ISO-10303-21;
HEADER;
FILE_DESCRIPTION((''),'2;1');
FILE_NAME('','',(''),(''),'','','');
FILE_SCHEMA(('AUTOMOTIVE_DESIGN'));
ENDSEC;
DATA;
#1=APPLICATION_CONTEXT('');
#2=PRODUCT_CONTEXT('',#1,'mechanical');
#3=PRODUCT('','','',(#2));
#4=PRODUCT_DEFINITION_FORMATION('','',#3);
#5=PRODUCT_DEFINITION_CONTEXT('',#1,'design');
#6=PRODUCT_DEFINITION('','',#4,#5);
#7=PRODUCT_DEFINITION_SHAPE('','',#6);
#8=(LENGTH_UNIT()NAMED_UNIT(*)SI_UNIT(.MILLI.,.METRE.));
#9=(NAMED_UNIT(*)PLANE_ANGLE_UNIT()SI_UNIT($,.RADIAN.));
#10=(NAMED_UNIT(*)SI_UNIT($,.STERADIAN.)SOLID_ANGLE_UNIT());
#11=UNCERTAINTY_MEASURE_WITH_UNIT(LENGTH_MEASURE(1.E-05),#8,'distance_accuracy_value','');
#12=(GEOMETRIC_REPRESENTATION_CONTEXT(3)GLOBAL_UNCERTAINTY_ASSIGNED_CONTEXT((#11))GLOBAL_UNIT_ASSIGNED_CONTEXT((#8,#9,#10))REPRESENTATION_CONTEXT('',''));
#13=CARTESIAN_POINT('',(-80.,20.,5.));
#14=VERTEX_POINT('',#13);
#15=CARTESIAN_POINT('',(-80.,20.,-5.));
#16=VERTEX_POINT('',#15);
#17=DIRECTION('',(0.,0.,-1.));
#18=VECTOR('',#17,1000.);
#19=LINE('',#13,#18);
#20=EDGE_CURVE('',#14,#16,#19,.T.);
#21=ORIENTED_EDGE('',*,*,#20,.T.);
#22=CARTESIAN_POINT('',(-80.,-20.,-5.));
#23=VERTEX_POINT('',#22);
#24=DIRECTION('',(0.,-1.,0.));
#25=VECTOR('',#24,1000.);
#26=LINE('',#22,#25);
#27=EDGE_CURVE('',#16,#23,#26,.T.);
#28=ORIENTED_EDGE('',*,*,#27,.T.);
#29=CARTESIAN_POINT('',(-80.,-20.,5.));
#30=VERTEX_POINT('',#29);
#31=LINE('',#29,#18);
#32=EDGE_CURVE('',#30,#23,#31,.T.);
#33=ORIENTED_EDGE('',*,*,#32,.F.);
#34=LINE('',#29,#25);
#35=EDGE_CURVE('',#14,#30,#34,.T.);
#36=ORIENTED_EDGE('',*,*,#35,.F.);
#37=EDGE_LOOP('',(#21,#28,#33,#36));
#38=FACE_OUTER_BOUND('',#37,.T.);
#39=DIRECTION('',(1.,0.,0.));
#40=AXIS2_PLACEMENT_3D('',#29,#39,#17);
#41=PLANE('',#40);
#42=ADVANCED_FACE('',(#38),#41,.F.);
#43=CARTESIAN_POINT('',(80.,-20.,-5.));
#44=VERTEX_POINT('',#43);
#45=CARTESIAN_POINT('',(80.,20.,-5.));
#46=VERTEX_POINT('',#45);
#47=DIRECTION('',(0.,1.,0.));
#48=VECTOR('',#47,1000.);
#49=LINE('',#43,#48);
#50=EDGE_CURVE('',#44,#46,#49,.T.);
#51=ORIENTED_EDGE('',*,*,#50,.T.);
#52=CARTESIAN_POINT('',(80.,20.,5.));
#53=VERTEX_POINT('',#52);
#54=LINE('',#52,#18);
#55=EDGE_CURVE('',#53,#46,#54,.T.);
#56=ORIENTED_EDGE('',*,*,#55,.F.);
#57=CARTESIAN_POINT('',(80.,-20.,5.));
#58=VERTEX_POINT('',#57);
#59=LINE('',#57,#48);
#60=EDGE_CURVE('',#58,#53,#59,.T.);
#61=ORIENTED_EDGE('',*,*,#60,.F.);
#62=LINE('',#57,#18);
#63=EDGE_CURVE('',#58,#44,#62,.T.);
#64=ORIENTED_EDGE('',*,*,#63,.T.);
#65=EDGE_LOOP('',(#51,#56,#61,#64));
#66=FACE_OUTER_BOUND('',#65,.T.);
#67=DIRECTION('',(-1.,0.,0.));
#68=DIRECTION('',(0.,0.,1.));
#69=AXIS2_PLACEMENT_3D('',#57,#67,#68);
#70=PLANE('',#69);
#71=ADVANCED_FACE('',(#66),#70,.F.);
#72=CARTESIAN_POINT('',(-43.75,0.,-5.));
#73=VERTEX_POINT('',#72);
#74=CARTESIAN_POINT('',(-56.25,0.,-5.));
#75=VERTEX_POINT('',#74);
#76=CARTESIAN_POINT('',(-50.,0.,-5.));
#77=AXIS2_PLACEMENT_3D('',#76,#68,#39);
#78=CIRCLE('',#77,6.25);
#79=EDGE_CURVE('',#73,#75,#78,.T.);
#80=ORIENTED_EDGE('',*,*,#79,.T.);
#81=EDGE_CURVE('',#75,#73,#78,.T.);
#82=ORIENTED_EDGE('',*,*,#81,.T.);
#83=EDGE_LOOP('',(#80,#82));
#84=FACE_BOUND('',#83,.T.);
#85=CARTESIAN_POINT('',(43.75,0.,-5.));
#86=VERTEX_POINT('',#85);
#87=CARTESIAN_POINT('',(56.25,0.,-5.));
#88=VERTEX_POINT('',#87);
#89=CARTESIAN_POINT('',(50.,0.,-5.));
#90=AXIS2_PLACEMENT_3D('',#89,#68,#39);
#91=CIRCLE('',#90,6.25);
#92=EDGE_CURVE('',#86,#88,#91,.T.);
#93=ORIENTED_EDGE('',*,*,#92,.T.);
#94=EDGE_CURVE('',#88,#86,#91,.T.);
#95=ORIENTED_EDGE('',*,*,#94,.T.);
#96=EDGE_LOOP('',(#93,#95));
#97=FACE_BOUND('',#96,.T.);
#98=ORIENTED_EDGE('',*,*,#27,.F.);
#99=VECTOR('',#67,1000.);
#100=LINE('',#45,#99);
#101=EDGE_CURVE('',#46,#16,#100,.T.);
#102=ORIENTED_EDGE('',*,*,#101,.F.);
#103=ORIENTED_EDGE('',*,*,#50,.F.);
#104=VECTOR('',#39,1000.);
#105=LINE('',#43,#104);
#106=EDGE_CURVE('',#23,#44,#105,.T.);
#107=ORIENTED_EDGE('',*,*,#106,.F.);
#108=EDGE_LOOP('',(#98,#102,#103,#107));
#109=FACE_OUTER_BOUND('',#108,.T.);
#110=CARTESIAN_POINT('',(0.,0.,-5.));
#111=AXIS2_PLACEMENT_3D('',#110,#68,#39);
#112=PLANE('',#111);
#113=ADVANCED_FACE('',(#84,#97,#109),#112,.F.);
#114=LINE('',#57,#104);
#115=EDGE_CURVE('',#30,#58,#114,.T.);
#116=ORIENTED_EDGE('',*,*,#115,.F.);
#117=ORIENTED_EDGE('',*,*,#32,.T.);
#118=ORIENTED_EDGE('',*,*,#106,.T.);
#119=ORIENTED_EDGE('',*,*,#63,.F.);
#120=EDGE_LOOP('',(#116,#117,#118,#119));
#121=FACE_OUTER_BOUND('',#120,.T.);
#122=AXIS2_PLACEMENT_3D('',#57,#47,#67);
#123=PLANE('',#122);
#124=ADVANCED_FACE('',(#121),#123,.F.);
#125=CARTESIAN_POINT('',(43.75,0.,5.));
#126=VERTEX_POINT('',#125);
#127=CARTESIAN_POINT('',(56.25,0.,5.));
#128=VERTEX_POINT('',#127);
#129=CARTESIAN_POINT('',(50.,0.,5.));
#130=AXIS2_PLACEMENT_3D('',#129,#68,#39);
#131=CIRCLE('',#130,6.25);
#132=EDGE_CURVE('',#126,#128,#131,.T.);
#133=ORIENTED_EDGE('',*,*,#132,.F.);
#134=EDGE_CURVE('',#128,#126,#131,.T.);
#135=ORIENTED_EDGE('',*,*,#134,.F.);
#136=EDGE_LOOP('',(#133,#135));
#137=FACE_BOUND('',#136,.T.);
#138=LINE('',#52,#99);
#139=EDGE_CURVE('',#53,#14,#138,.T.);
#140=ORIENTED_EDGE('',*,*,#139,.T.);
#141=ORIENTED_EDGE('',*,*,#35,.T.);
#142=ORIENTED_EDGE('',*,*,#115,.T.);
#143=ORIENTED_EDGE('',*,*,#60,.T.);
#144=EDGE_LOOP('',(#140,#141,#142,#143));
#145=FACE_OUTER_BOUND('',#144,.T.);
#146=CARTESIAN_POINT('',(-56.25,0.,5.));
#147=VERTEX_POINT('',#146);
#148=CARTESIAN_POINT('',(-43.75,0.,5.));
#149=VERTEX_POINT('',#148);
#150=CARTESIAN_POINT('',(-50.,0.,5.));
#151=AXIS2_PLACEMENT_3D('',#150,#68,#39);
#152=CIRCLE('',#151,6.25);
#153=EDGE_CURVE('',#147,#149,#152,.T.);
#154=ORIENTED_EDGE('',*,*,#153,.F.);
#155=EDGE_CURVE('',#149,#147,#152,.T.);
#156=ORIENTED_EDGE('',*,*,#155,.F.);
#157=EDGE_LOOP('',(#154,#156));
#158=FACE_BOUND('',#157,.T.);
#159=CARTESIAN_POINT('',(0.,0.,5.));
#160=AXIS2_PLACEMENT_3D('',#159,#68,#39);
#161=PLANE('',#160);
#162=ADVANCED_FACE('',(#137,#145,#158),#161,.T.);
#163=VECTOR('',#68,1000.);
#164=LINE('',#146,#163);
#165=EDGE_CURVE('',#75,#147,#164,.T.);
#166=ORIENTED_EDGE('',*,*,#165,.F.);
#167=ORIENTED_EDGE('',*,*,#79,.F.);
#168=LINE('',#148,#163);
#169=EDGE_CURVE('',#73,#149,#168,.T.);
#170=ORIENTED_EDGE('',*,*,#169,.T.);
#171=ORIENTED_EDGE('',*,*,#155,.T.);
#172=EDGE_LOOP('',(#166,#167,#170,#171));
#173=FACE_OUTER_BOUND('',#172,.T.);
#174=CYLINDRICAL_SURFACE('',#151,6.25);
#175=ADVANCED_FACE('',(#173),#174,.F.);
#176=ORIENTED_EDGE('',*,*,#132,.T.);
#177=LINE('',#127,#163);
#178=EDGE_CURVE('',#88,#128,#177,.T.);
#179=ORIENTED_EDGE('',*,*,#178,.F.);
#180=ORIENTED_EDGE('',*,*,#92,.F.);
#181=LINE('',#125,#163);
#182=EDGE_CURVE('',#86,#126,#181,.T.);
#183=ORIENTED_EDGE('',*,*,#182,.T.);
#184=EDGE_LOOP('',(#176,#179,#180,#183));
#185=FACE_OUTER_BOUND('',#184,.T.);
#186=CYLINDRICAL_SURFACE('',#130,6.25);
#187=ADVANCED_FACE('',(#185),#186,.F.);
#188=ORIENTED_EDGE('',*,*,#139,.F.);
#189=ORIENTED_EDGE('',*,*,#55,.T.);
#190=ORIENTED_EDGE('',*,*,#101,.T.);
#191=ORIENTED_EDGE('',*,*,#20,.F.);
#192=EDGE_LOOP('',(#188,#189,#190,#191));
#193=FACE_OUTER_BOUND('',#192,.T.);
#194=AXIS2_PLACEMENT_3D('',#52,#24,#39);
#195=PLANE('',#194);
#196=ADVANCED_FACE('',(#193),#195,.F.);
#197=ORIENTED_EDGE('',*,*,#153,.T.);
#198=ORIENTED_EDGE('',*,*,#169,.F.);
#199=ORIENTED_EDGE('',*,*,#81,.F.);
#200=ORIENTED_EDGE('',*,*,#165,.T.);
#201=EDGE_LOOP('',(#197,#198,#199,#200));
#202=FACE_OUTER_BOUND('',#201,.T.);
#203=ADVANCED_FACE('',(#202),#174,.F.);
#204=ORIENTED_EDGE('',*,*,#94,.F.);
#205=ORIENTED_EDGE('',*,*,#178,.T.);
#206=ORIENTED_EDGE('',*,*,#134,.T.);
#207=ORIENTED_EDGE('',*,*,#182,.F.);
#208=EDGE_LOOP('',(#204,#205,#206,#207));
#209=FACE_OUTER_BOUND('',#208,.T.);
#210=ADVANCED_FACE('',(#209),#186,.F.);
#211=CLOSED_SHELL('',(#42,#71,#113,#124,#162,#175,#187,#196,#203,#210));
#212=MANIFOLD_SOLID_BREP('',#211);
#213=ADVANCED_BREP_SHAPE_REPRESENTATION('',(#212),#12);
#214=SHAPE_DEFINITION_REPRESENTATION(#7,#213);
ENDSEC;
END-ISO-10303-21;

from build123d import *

# Parameters (mm, degrees)
SKETCH1_W                    = 160
SKETCH1_H                    = 40
BOSS_EXTRUDE1_DEPTH          = 5
F_12_5_12_5_DIAMETER_HOLE1_D = 12.5


with BuildPart() as part:
    # Sketch1 → Boss-Extrude1 (new, symmetric)
    with BuildSketch(Plane.XY):
        Rectangle(SKETCH1_W, SKETCH1_H)
    extrude(amount=BOSS_EXTRUDE1_DEPTH, both=True)

    # Ø12.5 (12.5) Diameter Hole1 (through all)
    with Locations(Plane.XY.offset(5)):
        with Locations((-50, 0), (50, 0)):
            Hole(F_12_5_12_5_DIAMETER_HOLE1_D / 2)


solid = part.part
